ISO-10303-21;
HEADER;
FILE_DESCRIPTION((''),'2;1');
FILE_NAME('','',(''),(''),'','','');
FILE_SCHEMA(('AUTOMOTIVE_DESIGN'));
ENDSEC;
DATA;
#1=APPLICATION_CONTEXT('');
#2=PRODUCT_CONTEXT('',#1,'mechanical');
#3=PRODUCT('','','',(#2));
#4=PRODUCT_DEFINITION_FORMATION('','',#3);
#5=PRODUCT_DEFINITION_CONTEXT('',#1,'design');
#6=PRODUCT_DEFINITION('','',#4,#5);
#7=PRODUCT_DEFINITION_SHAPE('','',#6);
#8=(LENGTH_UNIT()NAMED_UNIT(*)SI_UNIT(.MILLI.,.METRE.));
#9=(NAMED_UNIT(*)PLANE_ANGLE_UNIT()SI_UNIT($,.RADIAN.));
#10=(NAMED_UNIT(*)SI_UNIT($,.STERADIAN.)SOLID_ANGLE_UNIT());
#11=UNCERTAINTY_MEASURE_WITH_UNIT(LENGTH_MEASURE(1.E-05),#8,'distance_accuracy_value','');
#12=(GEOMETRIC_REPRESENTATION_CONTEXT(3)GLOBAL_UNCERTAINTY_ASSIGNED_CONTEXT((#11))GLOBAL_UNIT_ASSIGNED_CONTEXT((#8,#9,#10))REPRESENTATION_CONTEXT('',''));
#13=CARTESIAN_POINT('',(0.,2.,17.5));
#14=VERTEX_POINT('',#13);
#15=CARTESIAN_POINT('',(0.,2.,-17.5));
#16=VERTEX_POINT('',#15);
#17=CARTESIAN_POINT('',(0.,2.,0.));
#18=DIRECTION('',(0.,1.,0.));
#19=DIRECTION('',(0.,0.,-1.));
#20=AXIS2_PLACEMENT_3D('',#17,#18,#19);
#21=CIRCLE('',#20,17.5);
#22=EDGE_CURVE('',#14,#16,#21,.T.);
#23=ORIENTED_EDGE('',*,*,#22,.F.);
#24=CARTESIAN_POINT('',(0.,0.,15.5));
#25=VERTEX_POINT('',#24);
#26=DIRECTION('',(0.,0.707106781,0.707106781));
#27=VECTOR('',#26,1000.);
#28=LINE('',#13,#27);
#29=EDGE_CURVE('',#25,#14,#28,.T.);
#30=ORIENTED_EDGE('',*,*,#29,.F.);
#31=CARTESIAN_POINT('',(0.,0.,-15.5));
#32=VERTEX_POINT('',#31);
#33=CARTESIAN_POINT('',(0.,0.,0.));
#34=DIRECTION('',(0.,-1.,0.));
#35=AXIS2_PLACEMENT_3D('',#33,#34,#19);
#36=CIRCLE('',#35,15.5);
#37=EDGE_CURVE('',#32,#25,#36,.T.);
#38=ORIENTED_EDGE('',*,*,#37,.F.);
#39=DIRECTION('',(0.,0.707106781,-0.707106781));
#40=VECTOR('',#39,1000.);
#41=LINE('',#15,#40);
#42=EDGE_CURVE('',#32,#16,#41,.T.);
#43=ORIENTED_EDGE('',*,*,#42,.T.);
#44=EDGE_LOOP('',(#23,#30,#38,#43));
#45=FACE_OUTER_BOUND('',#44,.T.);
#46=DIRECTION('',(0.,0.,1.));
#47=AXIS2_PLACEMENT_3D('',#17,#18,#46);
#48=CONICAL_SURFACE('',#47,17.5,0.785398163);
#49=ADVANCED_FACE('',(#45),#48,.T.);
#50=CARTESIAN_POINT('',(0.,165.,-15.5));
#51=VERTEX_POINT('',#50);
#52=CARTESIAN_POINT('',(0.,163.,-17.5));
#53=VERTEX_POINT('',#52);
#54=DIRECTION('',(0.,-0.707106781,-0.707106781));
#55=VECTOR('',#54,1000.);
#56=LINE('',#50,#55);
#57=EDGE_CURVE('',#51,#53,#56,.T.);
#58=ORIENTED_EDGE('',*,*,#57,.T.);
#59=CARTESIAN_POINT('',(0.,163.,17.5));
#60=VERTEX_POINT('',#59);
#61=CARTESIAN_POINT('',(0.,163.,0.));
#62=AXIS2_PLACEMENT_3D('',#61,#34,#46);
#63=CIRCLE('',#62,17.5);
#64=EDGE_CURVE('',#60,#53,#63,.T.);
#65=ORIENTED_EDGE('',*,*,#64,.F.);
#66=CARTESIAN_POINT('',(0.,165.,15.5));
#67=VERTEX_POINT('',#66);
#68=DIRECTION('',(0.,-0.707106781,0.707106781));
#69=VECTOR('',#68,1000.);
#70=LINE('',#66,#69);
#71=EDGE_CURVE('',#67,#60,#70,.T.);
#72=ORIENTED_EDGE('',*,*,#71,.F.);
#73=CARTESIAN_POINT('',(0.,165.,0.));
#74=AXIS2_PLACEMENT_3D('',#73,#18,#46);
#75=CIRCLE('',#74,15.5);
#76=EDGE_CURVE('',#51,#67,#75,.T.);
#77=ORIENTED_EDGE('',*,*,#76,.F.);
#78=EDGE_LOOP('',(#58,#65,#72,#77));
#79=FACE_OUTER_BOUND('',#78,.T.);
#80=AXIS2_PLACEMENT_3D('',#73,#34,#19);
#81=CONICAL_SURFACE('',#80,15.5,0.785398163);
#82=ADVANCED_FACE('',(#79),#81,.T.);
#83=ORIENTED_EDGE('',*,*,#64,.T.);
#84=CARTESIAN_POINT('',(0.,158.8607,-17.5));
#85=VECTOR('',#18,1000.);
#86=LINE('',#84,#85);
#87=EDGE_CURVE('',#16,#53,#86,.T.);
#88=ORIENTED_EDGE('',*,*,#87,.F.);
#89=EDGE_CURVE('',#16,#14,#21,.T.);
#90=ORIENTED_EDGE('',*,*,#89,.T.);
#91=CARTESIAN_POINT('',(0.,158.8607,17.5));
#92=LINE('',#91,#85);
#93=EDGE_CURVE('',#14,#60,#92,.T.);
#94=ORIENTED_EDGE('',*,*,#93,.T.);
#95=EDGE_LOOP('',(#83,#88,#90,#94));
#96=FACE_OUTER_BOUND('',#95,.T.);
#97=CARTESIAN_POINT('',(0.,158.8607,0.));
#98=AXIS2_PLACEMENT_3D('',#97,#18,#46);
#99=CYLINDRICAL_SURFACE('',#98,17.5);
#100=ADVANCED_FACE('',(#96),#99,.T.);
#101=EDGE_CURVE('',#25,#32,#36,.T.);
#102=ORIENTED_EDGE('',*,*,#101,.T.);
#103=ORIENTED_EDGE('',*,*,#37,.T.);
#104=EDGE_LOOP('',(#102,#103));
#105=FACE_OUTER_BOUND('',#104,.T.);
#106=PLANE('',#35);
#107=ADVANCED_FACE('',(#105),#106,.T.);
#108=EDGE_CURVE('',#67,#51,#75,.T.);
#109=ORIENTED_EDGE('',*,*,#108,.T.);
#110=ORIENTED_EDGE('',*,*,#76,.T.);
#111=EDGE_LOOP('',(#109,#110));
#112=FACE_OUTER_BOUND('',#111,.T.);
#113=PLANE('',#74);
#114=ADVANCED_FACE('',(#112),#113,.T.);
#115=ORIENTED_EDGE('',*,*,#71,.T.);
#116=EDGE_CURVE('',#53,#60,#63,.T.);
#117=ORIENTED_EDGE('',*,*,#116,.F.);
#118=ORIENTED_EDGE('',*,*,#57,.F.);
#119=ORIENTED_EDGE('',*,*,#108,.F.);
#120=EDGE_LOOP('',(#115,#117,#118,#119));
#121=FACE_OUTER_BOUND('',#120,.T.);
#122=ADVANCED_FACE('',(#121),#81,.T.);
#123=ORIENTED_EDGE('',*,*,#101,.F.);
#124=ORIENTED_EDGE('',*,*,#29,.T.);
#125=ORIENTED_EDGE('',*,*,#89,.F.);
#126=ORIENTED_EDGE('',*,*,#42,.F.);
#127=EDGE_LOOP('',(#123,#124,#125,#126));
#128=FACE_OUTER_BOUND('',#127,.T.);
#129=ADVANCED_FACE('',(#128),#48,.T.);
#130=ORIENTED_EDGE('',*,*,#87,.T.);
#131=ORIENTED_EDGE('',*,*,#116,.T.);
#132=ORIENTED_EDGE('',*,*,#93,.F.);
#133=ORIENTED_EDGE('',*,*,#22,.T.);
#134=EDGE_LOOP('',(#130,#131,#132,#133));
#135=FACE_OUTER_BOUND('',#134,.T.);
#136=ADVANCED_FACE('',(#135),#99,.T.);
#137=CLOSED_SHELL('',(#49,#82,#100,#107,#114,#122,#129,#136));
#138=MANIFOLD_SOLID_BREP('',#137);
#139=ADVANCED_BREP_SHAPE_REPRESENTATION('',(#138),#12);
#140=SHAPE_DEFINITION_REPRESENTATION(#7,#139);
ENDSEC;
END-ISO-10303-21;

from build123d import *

# Parameters (mm, degrees)
SKETCH1_W     = 17.5
SKETCH1_H     = 165
CHAMFER1_SIZE = 2


with BuildPart() as part:
    # Sketch1 → Revolve1 (revolve)
    with BuildSketch(Plane.XY, mode=Mode.PRIVATE) as revolve1_sk:
        with Locations((-8.75, 82.5)):
            Rectangle(SKETCH1_W, SKETCH1_H)
    revolve(revolve1_sk.sketch.rotate(Axis((0, 158.86069982, 0), (0, -1, 0)), 270), axis=Axis((0, 158.86069982, 0), (0, -1, 0)))

    # Chamfer1
    chamfer1_edges = [part.edges().sort_by_distance(p)[0] for p in [
        (0, 0, -17.5),
        (0, 165, -17.5),
    ]]
    chamfer(chamfer1_edges, length=CHAMFER1_SIZE)


solid = part.part
